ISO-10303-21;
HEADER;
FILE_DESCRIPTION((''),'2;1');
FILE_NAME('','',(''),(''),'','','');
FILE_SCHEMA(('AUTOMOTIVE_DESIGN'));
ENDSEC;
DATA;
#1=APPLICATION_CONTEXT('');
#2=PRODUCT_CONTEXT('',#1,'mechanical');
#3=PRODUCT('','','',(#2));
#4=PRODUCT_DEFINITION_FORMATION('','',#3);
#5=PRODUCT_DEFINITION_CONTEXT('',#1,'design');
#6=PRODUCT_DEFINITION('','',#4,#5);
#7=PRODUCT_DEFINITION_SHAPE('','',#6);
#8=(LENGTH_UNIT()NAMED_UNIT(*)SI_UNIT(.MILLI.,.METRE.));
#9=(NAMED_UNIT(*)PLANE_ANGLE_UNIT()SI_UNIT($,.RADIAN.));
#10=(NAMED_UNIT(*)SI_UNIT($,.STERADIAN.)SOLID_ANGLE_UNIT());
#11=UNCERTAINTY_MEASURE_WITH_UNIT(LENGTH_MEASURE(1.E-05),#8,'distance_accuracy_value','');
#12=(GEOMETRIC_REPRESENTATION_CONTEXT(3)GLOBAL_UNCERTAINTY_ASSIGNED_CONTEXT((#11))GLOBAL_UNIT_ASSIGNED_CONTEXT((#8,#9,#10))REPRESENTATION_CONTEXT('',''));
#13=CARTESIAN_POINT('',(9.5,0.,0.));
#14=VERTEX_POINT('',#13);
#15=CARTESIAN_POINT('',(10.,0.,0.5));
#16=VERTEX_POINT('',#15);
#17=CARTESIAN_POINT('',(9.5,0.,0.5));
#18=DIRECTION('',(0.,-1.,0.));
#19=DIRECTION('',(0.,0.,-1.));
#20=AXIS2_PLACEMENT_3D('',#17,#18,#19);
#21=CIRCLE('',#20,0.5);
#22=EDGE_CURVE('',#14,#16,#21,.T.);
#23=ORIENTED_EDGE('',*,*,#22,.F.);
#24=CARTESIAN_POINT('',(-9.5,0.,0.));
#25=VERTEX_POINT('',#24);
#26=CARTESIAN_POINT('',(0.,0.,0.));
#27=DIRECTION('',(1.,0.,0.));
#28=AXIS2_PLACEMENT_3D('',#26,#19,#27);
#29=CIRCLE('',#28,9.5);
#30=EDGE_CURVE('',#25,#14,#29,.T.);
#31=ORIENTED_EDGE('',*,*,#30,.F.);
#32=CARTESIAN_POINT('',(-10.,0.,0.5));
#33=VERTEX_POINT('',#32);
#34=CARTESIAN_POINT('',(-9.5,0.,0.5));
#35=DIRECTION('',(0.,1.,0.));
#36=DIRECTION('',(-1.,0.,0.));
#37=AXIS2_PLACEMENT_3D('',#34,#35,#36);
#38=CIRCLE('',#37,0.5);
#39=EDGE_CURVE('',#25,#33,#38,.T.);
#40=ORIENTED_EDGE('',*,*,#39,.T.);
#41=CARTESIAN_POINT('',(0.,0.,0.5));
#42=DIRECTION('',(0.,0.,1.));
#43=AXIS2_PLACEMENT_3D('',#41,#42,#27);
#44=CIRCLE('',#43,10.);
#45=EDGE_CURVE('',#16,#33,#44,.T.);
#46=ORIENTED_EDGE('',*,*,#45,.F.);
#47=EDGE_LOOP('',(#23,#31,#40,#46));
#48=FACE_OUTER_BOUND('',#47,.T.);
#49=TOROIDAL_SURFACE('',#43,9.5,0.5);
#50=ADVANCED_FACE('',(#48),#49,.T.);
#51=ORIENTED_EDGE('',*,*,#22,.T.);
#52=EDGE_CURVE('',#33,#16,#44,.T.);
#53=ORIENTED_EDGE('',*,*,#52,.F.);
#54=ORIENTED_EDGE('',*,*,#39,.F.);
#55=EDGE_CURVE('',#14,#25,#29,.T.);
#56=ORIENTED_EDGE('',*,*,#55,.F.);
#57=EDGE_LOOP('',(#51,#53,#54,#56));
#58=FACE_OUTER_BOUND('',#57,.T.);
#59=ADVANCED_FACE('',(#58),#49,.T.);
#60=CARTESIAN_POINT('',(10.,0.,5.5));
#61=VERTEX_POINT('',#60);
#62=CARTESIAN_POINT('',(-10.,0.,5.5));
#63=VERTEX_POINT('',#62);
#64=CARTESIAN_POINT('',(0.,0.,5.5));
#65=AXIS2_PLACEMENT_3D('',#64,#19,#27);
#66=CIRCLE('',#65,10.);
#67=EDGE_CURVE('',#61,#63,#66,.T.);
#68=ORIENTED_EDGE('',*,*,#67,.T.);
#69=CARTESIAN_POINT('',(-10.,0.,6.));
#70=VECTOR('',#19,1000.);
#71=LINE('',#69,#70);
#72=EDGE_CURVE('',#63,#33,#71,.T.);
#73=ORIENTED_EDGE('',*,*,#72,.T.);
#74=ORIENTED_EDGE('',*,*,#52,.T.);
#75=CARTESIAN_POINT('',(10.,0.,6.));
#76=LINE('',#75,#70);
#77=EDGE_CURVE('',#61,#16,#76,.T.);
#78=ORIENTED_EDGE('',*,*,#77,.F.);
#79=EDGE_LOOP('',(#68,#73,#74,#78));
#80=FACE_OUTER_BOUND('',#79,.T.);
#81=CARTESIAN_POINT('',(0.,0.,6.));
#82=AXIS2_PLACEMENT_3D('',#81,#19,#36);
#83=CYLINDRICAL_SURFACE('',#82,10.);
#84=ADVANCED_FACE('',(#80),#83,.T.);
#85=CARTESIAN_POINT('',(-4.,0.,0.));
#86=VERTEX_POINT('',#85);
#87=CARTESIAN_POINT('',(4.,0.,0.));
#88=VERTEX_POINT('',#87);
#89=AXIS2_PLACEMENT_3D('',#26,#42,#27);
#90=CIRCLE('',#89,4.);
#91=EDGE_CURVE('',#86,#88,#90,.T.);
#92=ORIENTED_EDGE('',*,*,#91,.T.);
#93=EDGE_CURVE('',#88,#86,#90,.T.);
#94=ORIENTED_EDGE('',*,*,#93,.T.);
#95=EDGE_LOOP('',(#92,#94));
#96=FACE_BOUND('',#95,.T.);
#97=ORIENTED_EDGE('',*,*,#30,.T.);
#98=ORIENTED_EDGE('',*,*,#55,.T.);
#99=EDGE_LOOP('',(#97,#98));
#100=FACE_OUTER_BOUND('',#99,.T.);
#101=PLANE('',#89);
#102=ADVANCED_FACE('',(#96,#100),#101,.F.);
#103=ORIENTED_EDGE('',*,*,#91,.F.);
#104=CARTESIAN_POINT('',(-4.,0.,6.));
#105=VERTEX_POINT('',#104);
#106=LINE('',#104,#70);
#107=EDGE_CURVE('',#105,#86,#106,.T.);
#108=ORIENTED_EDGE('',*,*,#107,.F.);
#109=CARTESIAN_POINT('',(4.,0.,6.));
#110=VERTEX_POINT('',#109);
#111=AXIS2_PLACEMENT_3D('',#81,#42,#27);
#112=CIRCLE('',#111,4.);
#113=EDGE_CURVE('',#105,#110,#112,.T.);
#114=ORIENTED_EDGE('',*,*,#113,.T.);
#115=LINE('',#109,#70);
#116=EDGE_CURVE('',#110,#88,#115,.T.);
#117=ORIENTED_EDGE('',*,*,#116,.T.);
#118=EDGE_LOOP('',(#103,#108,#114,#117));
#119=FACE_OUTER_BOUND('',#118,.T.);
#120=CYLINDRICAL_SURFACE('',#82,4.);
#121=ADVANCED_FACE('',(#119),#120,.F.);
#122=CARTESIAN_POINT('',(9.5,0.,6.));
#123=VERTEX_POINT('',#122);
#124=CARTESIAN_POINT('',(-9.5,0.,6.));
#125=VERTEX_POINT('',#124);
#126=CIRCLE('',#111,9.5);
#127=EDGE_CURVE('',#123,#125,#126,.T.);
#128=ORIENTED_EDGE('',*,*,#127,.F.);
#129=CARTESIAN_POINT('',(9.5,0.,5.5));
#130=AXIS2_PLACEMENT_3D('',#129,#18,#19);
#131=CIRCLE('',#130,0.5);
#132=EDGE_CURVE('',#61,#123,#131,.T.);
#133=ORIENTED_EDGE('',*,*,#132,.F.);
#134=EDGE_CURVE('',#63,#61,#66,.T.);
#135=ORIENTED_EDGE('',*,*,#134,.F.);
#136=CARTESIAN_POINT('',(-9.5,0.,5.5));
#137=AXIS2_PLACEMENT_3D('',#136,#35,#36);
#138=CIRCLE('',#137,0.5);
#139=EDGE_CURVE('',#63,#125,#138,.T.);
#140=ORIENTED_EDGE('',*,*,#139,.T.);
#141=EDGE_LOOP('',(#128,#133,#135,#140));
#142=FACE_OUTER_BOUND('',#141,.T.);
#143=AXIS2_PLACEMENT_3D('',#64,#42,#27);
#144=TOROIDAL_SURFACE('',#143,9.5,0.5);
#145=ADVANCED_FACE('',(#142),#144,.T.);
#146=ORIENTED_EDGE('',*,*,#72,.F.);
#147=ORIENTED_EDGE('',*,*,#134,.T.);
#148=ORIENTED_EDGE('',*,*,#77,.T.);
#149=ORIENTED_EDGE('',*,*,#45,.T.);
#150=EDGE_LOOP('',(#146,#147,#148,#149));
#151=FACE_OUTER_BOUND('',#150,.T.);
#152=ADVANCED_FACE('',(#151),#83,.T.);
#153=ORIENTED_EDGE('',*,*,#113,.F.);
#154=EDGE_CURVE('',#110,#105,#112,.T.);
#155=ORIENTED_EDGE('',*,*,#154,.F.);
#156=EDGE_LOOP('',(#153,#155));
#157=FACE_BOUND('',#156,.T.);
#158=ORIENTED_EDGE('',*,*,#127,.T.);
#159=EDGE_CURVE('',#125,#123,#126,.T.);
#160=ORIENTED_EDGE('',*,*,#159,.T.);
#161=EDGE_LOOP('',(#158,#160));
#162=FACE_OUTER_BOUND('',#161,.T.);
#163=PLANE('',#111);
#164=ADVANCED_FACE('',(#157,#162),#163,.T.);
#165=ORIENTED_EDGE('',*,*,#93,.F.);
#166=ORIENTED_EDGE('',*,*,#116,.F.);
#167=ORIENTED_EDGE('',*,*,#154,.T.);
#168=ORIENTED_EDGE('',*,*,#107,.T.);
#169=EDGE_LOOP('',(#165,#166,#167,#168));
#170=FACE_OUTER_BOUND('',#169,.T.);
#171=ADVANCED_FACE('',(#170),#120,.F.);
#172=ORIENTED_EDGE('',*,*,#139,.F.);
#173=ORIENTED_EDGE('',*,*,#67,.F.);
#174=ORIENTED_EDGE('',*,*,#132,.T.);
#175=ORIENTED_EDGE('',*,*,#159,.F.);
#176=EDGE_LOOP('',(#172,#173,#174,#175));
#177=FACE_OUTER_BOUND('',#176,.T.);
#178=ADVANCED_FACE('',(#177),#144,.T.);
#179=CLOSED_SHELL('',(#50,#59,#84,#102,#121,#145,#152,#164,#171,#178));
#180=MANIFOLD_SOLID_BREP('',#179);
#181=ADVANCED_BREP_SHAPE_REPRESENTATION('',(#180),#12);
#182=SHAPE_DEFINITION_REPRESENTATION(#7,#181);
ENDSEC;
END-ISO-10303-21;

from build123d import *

# Parameters (mm, degrees)
SKETCH_1_R      = 10
SKETCH_1_R_2    = 4
EXTRUDE_1_DEPTH = 6
FILLET_1_R      = 0.5


with BuildPart() as part:
    # 草图1 → 凸台-拉伸1 (new body)
    with BuildSketch(Plane.XY):
        Circle(SKETCH_1_R)
        Circle(SKETCH_1_R_2, mode=Mode.SUBTRACT)
    extrude(amount=EXTRUDE_1_DEPTH)

    # 圆角1
    fillet_1_edges = [part.edges().sort_by_distance(p)[0] for p in [
        (-10, 0, 0),
        (-10, 0, 6),
    ]]
    fillet(fillet_1_edges, radius=FILLET_1_R)


solid = part.part
